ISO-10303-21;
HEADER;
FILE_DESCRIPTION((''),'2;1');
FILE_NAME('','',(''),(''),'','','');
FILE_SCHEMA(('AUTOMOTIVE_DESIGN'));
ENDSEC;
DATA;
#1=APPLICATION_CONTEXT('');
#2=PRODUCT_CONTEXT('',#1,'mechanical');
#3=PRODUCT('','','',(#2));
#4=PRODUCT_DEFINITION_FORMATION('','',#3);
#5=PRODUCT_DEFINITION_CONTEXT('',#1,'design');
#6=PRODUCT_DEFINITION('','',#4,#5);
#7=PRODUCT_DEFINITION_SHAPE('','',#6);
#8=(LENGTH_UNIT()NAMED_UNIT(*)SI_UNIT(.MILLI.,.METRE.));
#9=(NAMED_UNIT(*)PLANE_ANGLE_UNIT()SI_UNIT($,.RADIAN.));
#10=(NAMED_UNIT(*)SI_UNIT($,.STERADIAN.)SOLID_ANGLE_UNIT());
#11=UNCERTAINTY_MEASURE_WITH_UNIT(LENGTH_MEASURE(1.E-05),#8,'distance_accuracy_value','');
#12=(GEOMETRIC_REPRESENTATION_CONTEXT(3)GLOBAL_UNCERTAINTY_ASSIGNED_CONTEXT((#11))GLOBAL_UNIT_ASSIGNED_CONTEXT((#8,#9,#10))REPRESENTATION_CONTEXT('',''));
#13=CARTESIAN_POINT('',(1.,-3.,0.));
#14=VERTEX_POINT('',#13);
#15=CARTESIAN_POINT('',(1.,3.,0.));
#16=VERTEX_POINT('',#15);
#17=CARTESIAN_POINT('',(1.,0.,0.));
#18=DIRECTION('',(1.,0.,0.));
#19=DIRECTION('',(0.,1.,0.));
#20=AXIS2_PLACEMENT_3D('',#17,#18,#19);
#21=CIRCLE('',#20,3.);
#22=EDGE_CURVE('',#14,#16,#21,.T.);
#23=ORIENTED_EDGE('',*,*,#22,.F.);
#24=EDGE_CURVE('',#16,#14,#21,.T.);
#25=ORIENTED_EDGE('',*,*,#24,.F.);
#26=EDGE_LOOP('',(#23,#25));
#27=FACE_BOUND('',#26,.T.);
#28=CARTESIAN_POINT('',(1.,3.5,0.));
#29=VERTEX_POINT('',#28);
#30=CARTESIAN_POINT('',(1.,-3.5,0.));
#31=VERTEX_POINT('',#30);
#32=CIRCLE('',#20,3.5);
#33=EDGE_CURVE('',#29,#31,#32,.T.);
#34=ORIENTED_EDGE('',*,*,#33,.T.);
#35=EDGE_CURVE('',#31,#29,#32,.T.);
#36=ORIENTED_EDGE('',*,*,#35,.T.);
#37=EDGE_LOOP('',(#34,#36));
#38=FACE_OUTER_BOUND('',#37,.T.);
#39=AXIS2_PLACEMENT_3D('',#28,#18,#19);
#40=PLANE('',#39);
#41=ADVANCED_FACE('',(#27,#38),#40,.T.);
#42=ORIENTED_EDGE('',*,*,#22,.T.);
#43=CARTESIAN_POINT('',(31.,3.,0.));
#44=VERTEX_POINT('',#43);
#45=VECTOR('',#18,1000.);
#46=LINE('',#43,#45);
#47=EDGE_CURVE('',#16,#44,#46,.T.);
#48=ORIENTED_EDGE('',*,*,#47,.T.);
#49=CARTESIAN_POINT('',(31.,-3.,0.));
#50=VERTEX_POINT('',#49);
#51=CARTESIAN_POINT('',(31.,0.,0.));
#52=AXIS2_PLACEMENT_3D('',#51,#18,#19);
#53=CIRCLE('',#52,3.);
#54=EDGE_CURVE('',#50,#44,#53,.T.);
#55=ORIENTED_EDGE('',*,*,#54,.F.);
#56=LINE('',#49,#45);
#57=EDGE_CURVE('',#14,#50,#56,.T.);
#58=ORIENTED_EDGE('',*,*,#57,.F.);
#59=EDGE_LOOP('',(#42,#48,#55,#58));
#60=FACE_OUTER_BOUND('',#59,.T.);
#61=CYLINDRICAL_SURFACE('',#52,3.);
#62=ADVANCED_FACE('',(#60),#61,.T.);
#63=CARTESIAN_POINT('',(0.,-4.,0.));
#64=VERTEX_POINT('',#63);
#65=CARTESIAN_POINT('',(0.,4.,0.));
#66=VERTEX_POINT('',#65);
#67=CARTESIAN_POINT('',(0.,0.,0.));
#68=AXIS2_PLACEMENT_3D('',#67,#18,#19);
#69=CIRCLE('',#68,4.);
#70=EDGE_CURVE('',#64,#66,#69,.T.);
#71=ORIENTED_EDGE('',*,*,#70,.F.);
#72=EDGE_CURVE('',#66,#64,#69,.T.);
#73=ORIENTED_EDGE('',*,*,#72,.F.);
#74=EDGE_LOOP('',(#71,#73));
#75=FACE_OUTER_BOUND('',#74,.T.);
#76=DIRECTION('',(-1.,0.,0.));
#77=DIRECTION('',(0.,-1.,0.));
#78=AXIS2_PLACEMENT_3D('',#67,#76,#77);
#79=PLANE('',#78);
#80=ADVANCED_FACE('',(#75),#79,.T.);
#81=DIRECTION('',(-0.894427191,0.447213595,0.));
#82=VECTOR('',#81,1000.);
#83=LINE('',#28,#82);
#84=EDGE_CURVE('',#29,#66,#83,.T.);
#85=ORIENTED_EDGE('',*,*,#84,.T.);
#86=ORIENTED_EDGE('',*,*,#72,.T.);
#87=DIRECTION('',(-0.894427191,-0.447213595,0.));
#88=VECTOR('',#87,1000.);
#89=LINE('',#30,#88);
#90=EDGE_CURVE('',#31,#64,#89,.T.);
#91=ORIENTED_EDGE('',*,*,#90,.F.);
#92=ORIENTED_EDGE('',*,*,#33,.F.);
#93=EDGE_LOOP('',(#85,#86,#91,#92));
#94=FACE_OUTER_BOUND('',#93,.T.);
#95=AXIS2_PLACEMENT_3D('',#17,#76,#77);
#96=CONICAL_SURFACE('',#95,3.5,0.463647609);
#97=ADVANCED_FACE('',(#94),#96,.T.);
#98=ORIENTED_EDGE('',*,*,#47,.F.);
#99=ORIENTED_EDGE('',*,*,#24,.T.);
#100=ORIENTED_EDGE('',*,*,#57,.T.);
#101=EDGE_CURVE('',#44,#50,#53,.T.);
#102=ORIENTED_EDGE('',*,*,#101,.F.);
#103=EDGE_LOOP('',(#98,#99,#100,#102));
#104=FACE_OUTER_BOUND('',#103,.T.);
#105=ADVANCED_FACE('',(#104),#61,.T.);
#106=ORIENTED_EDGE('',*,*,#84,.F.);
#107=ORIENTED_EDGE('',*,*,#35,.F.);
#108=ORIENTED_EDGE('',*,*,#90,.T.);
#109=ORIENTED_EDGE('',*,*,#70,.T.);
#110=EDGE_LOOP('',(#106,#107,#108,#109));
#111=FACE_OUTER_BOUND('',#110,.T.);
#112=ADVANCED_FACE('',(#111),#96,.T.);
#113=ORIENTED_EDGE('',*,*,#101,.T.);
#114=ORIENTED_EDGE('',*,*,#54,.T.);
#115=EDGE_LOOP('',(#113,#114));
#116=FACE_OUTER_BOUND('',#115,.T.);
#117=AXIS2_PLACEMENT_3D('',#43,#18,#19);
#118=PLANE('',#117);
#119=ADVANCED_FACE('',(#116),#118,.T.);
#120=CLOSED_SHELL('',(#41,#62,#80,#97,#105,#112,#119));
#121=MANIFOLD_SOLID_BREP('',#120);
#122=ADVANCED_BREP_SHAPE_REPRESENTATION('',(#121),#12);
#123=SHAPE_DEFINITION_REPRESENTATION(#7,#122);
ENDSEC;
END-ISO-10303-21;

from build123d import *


with BuildPart() as part:
    # Sketch1 → Revolve1 (revolve)
    with BuildSketch(Plane.XY):
        Polygon((0, 0), (0, 4), (1, 3.5), (1, 3), (31, 3), (31, 0), align=None)
    revolve(axis=Axis((31, 0, 0), (-1, 0, 0)))


solid = part.part
